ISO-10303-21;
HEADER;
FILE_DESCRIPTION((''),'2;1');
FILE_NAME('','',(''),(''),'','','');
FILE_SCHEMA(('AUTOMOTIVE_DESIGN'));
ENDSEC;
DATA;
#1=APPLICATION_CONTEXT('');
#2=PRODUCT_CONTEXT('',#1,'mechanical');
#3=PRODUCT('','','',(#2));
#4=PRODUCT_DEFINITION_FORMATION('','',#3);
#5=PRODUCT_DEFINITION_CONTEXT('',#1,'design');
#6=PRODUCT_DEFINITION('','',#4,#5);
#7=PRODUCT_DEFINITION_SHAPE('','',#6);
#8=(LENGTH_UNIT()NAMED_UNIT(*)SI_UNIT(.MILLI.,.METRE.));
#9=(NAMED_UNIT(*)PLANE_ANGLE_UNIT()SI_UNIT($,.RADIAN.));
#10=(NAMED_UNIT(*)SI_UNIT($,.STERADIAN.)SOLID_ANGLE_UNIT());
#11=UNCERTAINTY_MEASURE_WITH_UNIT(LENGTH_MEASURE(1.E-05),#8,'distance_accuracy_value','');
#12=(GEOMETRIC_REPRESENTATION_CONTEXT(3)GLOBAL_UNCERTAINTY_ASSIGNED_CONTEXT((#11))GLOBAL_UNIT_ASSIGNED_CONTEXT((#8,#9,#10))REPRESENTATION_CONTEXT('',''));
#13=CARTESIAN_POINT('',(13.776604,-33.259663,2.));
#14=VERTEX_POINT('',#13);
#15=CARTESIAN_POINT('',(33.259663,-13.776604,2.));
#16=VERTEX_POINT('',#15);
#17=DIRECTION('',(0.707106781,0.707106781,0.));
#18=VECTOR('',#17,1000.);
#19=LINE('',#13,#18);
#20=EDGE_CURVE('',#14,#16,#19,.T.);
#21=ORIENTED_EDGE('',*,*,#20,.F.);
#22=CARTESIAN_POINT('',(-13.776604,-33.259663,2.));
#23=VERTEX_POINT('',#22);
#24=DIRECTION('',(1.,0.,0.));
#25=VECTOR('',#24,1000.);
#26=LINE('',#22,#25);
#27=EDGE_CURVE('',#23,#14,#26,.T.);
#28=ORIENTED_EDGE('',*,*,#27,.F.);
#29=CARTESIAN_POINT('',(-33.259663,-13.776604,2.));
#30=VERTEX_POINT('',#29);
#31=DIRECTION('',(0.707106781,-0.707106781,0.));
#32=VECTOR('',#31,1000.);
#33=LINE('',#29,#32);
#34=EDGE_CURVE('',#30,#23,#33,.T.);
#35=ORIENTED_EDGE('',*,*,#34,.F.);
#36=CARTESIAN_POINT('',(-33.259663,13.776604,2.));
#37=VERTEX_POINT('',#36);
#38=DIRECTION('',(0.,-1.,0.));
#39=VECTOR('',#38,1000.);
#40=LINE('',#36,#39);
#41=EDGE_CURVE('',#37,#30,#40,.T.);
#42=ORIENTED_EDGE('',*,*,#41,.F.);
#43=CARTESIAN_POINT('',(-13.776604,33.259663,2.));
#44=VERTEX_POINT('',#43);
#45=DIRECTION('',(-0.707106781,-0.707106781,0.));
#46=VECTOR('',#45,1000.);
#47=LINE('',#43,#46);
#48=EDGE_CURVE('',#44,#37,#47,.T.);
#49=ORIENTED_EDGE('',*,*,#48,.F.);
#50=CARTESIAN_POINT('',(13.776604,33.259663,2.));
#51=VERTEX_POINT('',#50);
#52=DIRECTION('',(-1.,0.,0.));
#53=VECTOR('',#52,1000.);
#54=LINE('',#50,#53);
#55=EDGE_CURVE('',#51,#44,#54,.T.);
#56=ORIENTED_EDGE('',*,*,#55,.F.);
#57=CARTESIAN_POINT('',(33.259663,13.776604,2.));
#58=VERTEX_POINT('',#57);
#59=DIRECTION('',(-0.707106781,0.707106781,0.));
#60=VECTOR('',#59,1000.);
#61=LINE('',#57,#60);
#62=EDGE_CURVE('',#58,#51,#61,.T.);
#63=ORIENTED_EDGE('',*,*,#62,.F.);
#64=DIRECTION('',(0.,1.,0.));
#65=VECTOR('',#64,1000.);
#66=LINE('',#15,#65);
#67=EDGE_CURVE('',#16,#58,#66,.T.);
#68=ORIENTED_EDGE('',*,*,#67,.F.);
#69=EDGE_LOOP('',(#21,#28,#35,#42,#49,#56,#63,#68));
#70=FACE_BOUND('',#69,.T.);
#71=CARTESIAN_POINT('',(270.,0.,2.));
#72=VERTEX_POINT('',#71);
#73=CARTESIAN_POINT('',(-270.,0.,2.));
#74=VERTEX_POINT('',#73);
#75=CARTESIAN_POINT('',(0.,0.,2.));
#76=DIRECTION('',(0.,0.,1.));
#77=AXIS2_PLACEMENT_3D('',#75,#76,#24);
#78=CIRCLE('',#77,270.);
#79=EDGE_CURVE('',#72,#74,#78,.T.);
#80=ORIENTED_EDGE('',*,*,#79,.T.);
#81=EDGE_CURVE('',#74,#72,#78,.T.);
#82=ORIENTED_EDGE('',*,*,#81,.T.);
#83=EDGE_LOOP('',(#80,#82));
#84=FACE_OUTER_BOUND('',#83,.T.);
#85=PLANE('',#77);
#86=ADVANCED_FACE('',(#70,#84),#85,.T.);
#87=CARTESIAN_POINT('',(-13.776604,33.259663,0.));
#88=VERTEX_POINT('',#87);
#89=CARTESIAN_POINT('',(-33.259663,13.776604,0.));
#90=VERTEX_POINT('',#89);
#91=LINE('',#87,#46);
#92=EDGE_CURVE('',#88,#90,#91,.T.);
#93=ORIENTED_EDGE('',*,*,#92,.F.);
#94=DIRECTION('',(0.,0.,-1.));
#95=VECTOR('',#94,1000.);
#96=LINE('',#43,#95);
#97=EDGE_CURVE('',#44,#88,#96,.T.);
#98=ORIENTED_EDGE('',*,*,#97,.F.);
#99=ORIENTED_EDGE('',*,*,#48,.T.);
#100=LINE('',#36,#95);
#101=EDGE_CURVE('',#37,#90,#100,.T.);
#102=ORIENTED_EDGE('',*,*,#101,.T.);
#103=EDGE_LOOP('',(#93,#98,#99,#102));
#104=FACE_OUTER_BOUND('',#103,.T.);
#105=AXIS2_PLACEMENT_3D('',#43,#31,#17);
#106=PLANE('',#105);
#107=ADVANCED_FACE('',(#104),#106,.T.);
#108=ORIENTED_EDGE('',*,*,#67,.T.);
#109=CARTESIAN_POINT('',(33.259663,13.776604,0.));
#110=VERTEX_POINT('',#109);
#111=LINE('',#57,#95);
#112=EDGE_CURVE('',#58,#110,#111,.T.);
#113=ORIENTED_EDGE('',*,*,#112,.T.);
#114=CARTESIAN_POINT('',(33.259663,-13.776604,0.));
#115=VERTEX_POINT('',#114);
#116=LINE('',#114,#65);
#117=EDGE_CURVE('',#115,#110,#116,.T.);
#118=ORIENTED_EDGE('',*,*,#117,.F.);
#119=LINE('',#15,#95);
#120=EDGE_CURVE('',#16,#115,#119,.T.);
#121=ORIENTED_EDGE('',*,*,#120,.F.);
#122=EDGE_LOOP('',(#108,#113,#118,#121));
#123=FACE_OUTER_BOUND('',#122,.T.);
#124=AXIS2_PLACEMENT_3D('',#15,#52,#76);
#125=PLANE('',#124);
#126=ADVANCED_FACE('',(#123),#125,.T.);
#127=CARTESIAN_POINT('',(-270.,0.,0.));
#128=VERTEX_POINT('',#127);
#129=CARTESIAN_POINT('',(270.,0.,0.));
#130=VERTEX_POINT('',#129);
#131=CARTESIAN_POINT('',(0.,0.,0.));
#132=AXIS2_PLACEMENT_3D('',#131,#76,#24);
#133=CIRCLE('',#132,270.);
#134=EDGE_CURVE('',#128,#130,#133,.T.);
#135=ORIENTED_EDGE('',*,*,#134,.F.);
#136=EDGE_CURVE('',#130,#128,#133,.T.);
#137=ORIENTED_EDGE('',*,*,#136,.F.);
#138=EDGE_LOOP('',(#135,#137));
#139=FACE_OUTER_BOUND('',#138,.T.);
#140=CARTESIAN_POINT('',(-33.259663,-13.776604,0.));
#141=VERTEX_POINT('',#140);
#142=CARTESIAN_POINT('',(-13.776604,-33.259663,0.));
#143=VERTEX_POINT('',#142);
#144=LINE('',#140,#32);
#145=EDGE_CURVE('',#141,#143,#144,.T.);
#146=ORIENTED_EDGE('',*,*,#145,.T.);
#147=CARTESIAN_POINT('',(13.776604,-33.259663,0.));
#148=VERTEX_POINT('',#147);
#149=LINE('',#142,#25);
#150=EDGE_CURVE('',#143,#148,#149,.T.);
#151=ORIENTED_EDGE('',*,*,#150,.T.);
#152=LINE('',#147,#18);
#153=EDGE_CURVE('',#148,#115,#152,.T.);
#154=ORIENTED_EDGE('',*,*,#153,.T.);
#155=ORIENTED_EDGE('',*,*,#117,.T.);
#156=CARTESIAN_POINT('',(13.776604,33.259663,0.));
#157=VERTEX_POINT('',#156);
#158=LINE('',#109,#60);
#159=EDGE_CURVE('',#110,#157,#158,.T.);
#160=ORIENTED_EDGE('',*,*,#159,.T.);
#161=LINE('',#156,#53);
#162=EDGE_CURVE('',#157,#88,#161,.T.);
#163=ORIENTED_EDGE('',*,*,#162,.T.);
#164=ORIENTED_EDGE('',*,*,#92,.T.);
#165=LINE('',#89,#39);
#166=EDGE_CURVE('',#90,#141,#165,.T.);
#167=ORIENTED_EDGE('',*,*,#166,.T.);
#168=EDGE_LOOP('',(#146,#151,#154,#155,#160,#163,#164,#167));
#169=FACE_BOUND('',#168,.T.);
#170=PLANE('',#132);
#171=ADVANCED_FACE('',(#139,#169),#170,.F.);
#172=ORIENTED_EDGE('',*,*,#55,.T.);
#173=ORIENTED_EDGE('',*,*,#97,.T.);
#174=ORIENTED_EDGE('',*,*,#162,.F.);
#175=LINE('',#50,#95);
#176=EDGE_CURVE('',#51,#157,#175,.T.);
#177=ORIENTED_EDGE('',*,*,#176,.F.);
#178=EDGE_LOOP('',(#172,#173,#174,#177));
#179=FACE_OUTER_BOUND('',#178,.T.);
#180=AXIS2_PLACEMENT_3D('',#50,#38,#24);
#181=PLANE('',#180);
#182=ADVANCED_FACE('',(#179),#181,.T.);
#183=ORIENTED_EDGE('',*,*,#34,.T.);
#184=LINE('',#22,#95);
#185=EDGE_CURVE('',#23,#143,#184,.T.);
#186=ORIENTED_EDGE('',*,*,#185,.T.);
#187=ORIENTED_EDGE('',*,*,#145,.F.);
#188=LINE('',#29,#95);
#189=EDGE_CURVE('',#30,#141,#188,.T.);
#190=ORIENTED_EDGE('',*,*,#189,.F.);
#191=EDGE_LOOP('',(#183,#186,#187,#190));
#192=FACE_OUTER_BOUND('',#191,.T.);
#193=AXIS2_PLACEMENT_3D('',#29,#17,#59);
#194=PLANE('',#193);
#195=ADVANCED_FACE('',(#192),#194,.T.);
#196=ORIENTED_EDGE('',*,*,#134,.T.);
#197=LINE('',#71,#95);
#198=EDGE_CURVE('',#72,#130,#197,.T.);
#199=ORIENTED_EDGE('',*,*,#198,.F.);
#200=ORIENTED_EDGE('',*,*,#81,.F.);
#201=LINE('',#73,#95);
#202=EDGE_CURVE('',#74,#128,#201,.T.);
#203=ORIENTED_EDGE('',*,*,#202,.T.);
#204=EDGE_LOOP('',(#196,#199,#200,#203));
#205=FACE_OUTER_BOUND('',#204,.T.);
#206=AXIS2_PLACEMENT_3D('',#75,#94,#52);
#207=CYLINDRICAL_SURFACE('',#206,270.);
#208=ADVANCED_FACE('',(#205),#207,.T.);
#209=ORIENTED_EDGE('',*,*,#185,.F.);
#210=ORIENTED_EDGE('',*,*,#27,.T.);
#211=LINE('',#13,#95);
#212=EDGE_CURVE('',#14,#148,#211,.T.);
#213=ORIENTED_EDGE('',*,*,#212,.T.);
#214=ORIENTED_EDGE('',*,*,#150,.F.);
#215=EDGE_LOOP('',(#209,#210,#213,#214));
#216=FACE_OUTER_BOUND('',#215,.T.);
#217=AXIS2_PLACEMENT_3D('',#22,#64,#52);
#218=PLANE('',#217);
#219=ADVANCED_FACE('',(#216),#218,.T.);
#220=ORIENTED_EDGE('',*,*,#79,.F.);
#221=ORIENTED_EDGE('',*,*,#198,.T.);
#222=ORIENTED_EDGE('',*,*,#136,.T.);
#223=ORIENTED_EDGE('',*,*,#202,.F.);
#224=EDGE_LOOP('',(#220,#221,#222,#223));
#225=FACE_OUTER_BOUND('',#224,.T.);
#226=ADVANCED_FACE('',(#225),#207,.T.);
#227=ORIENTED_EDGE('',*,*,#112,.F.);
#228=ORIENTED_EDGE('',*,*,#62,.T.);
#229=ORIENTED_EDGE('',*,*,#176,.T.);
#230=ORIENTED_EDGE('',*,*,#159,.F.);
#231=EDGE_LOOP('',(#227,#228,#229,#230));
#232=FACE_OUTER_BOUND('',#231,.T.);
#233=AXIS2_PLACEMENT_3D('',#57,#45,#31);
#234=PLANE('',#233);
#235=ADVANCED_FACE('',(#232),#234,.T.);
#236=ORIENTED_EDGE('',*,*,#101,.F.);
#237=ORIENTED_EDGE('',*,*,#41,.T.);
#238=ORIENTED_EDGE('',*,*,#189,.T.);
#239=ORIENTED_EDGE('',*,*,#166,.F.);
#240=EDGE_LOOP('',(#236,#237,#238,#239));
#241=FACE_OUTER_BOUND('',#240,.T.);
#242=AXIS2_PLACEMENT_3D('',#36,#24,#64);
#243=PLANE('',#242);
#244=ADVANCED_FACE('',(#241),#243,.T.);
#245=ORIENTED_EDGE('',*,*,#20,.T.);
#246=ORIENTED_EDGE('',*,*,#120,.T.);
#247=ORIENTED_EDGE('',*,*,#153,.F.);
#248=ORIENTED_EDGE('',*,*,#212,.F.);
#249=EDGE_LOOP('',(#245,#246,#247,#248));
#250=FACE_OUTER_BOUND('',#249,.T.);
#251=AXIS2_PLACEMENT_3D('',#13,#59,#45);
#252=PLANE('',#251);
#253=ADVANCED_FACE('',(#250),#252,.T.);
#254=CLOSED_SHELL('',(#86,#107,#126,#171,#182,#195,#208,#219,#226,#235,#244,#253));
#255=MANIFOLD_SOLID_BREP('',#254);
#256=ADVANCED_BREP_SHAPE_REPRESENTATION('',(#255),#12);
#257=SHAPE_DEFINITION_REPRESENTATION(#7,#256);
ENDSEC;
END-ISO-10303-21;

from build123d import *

# Parameters (mm, degrees)
SKETCH_1_R      = 270
EXTRUDE_1_DEPTH = 2


with BuildPart() as part:
    # 草图1 → 凸台-拉伸1 (new body)
    with BuildSketch(Plane.XY):
        Circle(SKETCH_1_R)
        Polygon((33.25966317, 13.776603565), (13.776603565, 33.25966317), (-13.776603565, 33.25966317), (-33.25966317, 13.776603565), (-33.25966317, -13.776603565), (-13.776603565, -33.25966317), (13.776603565, -33.25966317), (33.25966317, -13.776603565), align=None, mode=Mode.SUBTRACT)
    extrude(amount=EXTRUDE_1_DEPTH)


solid = part.part
